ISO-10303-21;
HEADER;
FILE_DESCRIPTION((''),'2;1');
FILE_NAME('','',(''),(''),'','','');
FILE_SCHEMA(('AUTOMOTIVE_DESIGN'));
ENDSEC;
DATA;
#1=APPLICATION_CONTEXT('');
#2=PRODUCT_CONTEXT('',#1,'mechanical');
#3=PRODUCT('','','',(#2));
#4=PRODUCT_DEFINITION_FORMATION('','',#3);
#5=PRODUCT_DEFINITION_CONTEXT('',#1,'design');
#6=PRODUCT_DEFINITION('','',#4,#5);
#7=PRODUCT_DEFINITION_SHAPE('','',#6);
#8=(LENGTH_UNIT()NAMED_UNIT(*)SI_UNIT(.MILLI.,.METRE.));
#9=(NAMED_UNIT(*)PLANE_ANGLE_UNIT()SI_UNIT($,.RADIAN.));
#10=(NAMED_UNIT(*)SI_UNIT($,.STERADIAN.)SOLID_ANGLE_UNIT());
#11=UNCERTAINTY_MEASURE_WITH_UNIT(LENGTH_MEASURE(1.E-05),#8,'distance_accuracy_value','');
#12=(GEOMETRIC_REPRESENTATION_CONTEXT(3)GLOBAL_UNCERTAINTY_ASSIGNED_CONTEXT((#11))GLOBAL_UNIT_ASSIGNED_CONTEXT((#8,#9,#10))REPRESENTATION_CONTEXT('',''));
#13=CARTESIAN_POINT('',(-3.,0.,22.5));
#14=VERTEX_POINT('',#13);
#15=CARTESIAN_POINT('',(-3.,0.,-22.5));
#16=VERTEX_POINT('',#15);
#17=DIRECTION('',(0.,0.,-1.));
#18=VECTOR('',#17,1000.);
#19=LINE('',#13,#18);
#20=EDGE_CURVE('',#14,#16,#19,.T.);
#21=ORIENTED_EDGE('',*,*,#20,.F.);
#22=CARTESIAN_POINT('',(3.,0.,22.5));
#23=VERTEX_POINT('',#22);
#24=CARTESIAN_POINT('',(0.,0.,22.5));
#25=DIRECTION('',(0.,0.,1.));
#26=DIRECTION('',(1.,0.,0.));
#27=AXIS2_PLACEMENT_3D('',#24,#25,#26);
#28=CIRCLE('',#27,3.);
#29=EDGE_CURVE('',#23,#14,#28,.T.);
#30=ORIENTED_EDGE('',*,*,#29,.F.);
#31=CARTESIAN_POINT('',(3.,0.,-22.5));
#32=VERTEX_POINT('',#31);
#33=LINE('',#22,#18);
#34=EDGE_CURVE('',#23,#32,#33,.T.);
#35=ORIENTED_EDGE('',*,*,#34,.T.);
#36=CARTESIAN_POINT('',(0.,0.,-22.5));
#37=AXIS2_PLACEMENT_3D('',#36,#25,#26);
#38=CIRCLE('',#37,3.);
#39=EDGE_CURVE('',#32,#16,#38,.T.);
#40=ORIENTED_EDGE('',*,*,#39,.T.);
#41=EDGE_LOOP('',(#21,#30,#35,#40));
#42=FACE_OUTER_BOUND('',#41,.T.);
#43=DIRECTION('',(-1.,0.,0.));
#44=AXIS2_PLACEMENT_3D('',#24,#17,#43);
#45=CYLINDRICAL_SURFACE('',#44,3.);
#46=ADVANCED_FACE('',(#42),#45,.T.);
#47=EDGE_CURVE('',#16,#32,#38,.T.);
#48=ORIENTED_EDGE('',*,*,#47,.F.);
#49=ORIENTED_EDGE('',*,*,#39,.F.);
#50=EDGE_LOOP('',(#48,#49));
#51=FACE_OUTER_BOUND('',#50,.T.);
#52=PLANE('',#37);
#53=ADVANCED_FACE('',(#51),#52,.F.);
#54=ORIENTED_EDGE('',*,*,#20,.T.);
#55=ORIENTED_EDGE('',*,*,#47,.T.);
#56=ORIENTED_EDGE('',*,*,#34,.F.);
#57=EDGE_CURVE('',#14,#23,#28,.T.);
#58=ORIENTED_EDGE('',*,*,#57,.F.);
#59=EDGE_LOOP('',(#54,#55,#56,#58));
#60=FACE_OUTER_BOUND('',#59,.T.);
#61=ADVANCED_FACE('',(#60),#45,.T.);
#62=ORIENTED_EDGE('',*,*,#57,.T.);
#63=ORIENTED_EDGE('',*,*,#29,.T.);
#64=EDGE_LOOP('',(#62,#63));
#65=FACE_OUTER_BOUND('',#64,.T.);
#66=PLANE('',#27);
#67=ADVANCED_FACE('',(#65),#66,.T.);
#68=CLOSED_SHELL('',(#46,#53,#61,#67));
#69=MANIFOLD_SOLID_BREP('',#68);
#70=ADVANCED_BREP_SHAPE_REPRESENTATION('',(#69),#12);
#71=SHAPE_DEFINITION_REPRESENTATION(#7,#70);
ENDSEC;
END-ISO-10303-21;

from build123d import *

# Parameters (mm, degrees)
SKETCH1_R           = 3
BOSS_EXTRUDE1_DEPTH = 22.5


with BuildPart() as part:
    # Sketch1 → Boss-Extrude1 (new, symmetric)
    with BuildSketch(Plane.XY):
        with Locations(Location((0, 0, 0), (0, 0, 180))):
            Circle(SKETCH1_R)
    extrude(amount=BOSS_EXTRUDE1_DEPTH, both=True)


solid = part.part
